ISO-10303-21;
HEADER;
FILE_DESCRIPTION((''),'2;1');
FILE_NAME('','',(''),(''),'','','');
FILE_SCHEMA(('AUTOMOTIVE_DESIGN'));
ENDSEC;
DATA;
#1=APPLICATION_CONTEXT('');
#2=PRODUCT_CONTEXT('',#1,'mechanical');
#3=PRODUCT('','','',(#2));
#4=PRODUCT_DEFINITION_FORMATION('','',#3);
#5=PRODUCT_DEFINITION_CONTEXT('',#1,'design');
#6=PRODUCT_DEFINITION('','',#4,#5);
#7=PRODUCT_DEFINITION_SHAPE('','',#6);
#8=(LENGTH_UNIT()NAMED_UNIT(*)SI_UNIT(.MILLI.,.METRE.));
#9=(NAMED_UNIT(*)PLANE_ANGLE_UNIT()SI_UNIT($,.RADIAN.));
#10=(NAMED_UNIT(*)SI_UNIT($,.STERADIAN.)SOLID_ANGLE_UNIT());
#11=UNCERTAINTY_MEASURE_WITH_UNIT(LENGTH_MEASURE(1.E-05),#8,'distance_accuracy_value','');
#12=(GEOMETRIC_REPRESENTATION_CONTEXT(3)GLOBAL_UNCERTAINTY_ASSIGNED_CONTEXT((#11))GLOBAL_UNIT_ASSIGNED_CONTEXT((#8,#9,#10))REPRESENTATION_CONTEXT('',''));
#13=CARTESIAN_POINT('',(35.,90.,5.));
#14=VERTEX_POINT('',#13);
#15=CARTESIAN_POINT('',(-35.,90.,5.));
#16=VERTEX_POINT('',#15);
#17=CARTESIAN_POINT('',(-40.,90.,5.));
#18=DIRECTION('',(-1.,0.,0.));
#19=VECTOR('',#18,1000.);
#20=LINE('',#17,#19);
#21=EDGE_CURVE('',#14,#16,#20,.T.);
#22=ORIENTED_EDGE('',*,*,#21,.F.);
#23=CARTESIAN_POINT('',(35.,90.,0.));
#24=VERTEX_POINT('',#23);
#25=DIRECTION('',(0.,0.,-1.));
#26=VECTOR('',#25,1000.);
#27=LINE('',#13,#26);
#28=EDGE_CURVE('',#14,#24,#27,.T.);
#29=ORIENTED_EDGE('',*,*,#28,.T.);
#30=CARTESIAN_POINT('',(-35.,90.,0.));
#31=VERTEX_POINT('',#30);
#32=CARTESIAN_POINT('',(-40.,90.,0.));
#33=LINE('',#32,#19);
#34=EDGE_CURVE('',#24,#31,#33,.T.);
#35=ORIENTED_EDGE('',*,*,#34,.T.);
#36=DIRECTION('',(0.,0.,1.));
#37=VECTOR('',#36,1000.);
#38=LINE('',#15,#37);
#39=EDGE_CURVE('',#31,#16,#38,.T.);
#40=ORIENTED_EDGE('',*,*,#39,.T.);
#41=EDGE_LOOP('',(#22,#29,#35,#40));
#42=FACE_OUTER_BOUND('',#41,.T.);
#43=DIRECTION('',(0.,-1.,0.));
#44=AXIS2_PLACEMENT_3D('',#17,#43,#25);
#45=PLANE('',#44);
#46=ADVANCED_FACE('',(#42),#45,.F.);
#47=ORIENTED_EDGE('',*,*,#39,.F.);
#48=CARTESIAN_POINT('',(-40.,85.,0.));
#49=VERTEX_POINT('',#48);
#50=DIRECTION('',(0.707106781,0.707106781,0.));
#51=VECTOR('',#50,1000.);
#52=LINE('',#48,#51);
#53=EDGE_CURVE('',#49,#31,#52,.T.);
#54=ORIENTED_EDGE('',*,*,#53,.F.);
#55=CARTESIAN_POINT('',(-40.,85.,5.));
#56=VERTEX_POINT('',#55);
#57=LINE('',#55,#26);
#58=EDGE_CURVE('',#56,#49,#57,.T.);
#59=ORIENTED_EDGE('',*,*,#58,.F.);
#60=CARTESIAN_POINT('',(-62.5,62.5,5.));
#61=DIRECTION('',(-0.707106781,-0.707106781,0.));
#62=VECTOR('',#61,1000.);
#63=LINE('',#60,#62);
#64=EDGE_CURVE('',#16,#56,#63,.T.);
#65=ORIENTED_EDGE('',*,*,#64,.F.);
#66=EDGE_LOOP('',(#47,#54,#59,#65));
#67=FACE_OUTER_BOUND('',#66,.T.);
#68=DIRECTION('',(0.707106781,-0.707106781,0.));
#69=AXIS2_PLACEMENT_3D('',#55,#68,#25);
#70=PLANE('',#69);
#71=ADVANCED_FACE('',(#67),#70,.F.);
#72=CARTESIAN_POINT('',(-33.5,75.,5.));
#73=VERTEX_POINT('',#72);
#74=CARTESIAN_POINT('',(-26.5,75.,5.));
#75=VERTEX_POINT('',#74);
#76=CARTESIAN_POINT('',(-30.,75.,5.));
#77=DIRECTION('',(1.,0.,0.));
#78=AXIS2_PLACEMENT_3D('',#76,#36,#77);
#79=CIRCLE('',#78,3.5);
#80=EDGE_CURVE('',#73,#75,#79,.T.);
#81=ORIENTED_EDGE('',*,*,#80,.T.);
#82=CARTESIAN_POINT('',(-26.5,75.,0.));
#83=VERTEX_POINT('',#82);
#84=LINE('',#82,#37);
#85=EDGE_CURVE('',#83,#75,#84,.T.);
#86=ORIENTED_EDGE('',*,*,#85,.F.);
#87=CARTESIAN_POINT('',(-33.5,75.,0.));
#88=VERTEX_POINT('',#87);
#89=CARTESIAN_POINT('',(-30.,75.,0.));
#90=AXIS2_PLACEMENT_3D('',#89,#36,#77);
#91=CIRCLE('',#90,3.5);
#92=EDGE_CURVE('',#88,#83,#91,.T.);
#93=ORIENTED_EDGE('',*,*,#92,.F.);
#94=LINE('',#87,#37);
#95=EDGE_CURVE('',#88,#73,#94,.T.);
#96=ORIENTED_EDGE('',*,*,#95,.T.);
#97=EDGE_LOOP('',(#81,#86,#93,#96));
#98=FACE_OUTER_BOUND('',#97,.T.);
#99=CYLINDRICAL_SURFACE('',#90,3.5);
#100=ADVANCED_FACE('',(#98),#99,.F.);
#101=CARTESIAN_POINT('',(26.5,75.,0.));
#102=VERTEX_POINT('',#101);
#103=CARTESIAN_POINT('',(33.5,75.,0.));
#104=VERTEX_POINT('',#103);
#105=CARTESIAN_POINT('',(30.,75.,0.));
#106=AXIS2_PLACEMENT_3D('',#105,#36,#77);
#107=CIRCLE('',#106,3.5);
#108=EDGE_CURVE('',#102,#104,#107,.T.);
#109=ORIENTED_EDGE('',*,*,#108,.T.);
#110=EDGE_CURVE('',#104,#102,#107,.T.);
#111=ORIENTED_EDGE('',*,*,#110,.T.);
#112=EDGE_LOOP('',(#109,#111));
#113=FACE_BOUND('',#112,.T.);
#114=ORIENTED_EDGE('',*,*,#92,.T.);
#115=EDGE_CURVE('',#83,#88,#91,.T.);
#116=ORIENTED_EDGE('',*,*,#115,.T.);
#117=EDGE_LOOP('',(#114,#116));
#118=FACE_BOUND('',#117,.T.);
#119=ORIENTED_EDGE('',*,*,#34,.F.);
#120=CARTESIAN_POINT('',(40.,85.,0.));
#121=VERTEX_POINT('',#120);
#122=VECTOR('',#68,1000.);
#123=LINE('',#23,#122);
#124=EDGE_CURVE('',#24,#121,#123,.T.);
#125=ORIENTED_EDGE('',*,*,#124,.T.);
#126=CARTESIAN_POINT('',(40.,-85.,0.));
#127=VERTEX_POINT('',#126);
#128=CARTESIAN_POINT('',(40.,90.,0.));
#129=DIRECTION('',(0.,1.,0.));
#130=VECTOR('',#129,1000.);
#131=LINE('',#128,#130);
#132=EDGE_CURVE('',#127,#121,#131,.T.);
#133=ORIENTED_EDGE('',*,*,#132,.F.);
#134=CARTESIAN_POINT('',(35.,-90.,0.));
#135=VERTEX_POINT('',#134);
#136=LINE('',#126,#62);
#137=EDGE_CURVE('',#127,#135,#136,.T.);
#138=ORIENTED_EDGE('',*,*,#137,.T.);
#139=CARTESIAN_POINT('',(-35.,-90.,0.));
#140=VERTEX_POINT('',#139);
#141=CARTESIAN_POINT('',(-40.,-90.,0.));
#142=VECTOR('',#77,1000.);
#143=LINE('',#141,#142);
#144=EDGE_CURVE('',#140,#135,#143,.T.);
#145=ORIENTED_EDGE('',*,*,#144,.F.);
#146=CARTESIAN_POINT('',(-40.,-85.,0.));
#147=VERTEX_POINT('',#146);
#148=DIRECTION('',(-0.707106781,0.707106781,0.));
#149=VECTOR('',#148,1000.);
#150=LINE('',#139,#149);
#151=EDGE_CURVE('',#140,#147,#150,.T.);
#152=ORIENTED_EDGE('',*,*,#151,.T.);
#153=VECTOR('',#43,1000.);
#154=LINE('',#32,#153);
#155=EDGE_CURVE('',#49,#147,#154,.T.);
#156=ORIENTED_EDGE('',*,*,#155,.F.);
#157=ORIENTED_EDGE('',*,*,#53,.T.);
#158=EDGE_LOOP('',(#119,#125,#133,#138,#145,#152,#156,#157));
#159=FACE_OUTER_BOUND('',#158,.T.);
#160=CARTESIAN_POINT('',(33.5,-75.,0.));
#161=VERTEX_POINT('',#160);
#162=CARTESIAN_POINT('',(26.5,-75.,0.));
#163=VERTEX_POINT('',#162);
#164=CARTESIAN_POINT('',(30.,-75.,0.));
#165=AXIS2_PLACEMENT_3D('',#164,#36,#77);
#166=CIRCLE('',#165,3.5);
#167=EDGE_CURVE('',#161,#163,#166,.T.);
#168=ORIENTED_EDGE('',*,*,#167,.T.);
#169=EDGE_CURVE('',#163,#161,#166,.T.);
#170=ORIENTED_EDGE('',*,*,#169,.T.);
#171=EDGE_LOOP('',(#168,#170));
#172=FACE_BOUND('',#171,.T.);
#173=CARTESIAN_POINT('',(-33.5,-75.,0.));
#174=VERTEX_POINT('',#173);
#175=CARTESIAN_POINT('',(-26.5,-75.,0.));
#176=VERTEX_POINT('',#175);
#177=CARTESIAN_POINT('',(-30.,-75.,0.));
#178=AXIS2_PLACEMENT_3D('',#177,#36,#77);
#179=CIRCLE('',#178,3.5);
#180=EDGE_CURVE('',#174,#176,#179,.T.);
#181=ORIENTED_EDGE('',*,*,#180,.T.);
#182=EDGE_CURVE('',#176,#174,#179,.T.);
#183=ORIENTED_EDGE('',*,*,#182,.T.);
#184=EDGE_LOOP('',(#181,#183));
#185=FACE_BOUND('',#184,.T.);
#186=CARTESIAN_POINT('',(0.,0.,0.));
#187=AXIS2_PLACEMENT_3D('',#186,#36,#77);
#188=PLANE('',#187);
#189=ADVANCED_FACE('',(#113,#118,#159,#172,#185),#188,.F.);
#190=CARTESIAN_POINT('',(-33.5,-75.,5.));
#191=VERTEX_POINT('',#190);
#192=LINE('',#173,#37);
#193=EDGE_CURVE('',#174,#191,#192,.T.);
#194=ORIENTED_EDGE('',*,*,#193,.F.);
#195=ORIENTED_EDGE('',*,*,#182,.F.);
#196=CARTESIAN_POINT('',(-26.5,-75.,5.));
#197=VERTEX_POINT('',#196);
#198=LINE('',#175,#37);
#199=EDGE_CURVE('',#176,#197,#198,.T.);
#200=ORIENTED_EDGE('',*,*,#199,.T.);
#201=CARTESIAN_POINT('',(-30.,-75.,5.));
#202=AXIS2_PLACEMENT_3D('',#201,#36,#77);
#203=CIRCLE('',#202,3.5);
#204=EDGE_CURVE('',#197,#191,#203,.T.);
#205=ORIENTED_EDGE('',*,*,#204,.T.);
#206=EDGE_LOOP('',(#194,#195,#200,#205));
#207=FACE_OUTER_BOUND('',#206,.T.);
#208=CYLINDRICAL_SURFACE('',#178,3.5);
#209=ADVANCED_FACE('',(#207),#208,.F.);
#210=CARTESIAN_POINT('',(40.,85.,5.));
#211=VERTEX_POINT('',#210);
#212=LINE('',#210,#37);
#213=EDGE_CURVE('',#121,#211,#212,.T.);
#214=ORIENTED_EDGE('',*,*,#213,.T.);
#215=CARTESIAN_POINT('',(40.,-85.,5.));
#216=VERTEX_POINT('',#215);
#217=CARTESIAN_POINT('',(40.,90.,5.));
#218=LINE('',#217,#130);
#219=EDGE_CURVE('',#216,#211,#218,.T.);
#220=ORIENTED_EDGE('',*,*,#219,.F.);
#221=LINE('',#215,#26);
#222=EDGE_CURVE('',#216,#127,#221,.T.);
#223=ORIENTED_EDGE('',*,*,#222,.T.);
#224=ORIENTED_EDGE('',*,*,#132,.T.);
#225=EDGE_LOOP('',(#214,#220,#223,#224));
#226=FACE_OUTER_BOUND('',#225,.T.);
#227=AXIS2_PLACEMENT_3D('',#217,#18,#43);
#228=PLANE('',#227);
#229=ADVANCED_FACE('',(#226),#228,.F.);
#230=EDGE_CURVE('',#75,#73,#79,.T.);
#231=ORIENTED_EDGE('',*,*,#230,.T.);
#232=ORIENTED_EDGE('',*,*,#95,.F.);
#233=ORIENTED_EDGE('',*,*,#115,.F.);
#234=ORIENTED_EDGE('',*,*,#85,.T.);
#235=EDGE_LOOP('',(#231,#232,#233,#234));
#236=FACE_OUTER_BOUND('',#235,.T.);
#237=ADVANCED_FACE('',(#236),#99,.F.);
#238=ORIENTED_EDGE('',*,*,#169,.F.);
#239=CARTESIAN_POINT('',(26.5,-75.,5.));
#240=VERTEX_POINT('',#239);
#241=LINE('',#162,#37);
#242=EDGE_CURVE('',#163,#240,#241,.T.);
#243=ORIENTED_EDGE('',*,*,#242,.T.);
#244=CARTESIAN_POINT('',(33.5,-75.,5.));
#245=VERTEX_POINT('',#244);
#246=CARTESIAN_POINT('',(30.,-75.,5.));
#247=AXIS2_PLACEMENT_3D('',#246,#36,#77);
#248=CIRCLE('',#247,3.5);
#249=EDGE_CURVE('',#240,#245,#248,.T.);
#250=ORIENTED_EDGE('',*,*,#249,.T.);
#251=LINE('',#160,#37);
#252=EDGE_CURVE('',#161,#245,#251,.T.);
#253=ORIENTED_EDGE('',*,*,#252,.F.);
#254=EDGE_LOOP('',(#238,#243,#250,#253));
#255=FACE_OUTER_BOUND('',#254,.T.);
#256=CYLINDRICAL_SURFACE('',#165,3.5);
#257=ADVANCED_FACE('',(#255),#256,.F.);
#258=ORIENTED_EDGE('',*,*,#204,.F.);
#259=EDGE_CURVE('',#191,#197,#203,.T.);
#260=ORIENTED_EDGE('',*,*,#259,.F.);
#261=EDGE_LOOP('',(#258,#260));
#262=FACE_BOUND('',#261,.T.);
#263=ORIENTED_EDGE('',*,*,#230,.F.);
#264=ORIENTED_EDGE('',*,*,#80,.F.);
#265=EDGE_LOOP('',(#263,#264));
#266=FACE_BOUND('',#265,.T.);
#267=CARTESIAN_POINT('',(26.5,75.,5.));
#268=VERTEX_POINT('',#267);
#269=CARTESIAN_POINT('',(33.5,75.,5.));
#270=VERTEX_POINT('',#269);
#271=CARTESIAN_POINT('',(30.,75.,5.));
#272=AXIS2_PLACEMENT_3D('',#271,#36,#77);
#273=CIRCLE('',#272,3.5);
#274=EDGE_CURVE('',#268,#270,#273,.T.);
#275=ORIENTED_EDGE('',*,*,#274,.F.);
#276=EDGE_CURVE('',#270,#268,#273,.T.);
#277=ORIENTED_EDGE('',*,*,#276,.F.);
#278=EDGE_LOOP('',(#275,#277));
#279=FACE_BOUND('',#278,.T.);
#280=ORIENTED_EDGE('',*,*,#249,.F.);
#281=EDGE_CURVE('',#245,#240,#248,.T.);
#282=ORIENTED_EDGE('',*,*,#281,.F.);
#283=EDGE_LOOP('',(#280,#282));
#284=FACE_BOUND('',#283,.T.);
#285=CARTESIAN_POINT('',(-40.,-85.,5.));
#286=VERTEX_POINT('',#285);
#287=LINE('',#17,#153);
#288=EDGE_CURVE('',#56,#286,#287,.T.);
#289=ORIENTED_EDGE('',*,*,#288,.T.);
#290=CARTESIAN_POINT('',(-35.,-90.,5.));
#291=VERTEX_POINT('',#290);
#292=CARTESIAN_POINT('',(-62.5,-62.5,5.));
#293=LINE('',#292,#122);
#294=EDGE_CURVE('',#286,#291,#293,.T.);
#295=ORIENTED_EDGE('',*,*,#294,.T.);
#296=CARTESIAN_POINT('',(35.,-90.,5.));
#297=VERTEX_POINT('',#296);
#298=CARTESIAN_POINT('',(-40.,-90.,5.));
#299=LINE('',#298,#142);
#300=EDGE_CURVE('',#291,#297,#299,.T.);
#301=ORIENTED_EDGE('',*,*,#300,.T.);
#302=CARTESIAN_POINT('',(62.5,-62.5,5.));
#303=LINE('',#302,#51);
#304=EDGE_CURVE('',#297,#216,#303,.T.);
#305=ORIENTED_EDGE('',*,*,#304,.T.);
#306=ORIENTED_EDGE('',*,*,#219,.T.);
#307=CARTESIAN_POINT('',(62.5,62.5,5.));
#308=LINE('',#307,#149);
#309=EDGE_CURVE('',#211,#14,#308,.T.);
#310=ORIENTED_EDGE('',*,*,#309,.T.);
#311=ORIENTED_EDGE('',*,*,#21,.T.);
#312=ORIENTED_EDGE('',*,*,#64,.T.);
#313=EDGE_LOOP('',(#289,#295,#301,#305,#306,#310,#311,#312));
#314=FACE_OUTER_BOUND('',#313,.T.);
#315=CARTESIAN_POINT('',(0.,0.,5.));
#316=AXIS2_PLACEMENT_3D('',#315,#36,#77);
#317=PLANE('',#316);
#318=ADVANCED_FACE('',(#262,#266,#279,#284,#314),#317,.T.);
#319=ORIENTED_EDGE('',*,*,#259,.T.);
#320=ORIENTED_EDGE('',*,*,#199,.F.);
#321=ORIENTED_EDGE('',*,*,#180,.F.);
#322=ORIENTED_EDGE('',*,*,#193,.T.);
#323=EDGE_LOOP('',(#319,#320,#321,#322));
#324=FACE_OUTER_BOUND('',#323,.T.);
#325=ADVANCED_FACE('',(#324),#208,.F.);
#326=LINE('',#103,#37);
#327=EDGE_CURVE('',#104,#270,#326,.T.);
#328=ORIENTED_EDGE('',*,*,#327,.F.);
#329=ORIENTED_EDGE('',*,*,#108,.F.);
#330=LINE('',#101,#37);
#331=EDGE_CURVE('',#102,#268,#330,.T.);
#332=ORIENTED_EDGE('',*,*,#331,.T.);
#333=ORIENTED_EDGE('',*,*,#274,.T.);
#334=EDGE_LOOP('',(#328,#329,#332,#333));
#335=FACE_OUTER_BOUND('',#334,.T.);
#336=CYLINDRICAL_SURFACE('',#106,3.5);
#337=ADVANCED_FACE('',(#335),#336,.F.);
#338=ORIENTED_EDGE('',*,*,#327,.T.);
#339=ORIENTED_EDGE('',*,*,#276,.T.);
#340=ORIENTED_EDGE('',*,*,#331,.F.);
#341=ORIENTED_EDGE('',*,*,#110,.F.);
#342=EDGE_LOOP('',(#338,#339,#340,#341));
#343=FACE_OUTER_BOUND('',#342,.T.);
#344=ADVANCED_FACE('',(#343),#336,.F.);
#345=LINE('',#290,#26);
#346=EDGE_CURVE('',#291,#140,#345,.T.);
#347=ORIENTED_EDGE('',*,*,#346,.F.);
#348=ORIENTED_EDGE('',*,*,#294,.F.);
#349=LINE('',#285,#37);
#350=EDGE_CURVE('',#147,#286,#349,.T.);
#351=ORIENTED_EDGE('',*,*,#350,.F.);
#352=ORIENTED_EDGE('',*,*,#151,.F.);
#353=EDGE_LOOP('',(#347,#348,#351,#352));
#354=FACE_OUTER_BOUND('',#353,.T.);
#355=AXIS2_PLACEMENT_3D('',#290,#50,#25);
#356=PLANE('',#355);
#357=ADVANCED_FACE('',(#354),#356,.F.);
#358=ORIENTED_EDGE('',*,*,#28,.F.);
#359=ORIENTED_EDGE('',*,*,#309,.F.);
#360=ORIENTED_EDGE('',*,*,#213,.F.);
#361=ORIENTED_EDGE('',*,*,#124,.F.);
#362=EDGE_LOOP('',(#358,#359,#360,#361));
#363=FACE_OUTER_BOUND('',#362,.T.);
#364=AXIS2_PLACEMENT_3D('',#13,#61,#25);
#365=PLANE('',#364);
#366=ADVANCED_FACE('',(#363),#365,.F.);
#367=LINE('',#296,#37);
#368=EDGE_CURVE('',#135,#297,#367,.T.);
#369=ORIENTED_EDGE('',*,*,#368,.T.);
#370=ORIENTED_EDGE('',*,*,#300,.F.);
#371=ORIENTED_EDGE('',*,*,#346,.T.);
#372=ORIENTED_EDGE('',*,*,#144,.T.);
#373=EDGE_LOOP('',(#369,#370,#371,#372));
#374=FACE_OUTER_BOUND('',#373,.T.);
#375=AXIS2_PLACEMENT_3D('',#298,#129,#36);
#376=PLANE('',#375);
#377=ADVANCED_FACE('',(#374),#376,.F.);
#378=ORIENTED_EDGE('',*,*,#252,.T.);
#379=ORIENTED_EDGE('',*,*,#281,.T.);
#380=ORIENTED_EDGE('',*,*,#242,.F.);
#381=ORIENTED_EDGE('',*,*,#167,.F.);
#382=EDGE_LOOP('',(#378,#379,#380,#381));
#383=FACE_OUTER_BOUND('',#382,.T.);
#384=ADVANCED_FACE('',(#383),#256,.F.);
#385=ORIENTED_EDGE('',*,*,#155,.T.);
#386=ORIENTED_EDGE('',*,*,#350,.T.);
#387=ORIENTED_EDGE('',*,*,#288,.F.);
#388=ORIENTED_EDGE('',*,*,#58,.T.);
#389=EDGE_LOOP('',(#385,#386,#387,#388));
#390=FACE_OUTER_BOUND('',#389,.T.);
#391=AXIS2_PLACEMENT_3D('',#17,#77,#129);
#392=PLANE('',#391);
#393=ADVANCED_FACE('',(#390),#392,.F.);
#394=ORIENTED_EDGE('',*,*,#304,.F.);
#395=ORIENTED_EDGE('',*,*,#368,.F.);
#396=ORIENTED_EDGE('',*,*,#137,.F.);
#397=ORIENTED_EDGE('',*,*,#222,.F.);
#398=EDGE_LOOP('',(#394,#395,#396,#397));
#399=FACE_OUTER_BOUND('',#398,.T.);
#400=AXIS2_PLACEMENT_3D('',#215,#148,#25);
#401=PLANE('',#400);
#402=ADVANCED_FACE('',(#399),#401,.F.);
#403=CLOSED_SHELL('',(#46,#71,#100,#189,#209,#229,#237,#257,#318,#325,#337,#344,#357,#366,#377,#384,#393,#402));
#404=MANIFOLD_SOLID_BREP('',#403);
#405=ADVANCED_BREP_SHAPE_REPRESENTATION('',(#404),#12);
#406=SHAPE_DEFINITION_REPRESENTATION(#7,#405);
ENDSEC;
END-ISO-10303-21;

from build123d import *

# Parameters (mm, degrees)
SKETCH_1_W          = 80
SKETCH_1_H          = 180
EXTRUDE_1_DEPTH     = 5
CHAMFER_1_SIZE      = 5
SKETCH_2_R          = 3.5
CUT_EXTRUDE_1_DEPTH = 5


with BuildPart() as part:
    # 草图1 → 凸台-拉伸1 (new body)
    with BuildSketch(Plane.XY):
        Rectangle(SKETCH_1_W, SKETCH_1_H)
    extrude(amount=EXTRUDE_1_DEPTH)

    # 倒角1
    chamfer_1_edges = [part.edges().sort_by_distance(p)[0] for p in [
        (40, -90, 2.5),
        (-40, -90, 2.5),
        (-40, 90, 2.5),
        (40, 90, 2.5),
    ]]
    chamfer(chamfer_1_edges, length=CHAMFER_1_SIZE)

    # 草图2 → 切除-拉伸1 (cut)
    with BuildSketch(Plane.XY.offset(5)):
        with Locations((-30, 75)):
            Circle(SKETCH_2_R)
        with Locations((30, 75)):
            Circle(SKETCH_2_R)
        with Locations((-30, -75)):
            Circle(SKETCH_2_R)
        with Locations((30, -75)):
            Circle(SKETCH_2_R)
    extrude(amount=-CUT_EXTRUDE_1_DEPTH, mode=Mode.SUBTRACT)


solid = part.part
